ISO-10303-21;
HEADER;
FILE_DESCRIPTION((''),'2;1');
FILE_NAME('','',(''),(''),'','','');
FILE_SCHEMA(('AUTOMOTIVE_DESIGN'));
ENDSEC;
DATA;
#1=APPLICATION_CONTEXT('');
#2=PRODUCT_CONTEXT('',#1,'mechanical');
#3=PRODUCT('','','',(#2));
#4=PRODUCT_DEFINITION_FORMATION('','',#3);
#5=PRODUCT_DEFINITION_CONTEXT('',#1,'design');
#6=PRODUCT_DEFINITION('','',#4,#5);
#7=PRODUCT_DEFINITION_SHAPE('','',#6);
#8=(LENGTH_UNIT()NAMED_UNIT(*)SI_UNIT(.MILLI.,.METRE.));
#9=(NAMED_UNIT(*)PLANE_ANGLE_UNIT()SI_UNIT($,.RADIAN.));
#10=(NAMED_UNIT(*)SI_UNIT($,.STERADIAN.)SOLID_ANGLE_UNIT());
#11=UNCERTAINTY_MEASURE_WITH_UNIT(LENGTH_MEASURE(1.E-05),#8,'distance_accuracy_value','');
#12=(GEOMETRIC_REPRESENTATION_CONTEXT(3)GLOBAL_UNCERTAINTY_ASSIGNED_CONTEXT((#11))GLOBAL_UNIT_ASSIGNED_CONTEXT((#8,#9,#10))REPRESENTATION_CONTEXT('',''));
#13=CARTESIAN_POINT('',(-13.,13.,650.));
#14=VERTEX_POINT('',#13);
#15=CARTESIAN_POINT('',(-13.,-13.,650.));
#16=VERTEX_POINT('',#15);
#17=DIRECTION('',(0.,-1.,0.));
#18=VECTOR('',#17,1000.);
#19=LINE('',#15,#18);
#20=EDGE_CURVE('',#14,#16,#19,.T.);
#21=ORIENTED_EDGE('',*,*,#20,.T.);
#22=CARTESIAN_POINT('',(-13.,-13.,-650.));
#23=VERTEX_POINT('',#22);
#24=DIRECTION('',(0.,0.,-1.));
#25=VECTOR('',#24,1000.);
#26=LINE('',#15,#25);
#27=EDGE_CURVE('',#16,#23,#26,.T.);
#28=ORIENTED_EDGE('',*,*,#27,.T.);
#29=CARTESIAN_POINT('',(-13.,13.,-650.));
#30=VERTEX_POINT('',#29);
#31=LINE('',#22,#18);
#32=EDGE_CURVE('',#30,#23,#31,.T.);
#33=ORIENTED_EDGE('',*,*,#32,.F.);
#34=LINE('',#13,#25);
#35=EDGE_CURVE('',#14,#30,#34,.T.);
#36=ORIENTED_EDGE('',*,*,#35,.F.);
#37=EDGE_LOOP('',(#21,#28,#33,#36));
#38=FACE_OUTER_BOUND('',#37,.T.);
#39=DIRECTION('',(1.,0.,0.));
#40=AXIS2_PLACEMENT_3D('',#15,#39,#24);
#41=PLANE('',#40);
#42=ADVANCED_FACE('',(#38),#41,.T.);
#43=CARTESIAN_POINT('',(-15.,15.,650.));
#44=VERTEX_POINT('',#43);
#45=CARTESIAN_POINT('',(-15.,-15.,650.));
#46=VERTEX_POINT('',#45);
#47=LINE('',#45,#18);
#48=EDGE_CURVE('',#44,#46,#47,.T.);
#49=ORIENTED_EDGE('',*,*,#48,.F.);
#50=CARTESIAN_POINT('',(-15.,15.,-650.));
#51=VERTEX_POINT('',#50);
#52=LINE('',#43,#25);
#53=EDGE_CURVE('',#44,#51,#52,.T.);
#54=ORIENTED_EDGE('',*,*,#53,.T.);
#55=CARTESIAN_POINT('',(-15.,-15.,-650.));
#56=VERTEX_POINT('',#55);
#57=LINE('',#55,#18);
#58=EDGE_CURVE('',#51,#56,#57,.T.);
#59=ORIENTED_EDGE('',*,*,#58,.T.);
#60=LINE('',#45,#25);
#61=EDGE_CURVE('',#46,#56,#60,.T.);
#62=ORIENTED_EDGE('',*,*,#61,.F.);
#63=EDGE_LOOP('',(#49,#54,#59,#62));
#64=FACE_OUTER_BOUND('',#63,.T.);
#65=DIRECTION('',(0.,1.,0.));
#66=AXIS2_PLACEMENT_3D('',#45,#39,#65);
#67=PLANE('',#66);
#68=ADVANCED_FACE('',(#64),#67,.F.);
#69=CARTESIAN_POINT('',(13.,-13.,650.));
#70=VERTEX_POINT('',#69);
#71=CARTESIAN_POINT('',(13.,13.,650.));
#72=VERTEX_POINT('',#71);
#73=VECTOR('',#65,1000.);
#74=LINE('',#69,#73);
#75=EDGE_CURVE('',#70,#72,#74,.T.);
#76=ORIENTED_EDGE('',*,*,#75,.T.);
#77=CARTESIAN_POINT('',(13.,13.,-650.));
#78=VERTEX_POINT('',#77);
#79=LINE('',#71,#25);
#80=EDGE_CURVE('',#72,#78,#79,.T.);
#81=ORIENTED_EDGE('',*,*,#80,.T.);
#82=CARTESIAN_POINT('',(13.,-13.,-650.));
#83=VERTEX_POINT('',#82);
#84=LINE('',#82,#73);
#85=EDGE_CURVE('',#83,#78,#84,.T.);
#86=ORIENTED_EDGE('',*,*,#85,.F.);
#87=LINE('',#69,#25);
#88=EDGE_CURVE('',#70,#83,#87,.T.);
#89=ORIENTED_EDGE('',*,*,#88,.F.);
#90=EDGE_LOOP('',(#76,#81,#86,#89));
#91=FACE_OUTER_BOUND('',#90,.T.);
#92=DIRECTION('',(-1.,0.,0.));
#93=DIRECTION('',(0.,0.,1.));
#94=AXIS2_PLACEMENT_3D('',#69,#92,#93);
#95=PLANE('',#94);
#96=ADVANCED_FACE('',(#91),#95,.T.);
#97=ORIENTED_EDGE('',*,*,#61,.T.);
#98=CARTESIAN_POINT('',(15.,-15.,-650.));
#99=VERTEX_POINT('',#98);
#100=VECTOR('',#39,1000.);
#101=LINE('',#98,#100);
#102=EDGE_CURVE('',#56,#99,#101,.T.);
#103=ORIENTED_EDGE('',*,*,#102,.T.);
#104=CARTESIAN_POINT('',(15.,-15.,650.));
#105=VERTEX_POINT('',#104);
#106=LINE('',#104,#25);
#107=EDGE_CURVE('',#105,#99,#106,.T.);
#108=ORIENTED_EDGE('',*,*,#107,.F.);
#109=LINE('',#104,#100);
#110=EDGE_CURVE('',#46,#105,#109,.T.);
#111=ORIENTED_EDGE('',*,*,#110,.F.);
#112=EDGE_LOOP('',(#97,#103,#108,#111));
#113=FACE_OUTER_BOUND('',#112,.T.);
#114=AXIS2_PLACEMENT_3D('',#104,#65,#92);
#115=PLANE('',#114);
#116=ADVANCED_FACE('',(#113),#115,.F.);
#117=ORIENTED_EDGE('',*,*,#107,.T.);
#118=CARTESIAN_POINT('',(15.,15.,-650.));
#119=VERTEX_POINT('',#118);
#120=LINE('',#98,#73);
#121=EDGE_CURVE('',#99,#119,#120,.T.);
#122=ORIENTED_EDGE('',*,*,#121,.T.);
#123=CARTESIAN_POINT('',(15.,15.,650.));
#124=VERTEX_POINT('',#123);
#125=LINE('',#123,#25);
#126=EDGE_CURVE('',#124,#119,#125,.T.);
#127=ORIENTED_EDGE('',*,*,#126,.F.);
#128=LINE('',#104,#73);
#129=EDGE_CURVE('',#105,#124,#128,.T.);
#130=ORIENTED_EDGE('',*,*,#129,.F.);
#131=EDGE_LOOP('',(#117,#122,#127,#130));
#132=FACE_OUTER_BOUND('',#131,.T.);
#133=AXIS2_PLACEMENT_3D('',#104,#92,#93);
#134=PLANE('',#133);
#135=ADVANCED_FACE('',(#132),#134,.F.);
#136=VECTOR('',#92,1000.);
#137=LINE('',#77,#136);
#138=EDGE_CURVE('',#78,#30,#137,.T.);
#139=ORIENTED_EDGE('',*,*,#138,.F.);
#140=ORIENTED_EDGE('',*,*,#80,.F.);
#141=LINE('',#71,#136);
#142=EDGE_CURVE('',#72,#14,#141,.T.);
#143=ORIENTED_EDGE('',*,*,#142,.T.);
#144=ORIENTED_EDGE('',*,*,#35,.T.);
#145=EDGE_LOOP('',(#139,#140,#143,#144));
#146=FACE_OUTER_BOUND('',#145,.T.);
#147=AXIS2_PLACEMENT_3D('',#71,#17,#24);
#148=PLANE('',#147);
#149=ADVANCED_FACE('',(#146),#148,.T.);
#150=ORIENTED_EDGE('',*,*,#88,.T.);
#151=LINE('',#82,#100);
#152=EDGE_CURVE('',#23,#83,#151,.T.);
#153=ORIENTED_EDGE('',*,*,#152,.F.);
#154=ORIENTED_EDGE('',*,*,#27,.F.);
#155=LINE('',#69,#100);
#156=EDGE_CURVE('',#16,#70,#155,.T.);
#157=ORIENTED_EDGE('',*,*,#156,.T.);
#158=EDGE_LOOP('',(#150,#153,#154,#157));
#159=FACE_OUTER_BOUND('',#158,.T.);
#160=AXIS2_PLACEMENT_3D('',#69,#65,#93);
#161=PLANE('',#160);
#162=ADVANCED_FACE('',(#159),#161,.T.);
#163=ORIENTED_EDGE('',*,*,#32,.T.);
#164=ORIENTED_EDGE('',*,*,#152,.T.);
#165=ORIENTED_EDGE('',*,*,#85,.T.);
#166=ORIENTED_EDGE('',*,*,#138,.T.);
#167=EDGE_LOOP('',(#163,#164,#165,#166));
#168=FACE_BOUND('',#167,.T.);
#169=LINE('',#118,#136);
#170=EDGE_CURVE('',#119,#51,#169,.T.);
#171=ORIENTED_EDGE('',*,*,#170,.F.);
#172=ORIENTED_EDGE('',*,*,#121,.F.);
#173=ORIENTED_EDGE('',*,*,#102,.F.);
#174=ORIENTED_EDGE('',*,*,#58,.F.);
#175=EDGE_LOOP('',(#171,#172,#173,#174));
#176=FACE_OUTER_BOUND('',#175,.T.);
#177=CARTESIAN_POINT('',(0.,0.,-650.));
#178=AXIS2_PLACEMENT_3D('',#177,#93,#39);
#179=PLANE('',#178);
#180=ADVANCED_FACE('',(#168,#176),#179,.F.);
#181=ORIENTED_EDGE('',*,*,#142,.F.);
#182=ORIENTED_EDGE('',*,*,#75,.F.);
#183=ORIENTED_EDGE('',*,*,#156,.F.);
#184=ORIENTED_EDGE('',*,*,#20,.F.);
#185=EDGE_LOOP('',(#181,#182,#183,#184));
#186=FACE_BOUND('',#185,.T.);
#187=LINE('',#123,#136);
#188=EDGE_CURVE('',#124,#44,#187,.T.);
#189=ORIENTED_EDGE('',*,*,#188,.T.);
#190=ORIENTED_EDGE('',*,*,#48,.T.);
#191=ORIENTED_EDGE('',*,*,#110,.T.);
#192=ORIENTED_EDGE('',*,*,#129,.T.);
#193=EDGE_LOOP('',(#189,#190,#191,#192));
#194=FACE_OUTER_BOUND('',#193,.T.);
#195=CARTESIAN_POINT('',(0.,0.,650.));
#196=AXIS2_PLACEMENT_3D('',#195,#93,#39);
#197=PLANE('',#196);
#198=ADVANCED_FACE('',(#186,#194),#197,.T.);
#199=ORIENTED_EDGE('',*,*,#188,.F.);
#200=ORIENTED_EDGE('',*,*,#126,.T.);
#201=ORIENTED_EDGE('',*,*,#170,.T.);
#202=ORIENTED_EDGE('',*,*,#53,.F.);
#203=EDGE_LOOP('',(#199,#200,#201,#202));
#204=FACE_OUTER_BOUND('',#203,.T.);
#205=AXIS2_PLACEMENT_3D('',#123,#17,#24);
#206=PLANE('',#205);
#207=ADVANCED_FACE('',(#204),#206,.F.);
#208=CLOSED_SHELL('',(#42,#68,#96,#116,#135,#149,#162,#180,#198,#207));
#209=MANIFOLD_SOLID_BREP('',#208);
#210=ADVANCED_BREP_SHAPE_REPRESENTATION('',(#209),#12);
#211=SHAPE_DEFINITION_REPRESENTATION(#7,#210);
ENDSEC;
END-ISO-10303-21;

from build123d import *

# Parameters (mm, degrees)
SKETCH_1_W      = 30
SKETCH_1_H      = 30
SKETCH_1_W_2    = 26
SKETCH_1_H_2    = 26
EXTRUDE_1_DEPTH = 650


with BuildPart() as part:
    # 草图1 → 凸台-拉伸1 (new, symmetric)
    with BuildSketch(Plane.XY):
        Rectangle(SKETCH_1_W, SKETCH_1_H)
        Rectangle(SKETCH_1_W_2, SKETCH_1_H_2, mode=Mode.SUBTRACT)
    extrude(amount=EXTRUDE_1_DEPTH, both=True)


solid = part.part
